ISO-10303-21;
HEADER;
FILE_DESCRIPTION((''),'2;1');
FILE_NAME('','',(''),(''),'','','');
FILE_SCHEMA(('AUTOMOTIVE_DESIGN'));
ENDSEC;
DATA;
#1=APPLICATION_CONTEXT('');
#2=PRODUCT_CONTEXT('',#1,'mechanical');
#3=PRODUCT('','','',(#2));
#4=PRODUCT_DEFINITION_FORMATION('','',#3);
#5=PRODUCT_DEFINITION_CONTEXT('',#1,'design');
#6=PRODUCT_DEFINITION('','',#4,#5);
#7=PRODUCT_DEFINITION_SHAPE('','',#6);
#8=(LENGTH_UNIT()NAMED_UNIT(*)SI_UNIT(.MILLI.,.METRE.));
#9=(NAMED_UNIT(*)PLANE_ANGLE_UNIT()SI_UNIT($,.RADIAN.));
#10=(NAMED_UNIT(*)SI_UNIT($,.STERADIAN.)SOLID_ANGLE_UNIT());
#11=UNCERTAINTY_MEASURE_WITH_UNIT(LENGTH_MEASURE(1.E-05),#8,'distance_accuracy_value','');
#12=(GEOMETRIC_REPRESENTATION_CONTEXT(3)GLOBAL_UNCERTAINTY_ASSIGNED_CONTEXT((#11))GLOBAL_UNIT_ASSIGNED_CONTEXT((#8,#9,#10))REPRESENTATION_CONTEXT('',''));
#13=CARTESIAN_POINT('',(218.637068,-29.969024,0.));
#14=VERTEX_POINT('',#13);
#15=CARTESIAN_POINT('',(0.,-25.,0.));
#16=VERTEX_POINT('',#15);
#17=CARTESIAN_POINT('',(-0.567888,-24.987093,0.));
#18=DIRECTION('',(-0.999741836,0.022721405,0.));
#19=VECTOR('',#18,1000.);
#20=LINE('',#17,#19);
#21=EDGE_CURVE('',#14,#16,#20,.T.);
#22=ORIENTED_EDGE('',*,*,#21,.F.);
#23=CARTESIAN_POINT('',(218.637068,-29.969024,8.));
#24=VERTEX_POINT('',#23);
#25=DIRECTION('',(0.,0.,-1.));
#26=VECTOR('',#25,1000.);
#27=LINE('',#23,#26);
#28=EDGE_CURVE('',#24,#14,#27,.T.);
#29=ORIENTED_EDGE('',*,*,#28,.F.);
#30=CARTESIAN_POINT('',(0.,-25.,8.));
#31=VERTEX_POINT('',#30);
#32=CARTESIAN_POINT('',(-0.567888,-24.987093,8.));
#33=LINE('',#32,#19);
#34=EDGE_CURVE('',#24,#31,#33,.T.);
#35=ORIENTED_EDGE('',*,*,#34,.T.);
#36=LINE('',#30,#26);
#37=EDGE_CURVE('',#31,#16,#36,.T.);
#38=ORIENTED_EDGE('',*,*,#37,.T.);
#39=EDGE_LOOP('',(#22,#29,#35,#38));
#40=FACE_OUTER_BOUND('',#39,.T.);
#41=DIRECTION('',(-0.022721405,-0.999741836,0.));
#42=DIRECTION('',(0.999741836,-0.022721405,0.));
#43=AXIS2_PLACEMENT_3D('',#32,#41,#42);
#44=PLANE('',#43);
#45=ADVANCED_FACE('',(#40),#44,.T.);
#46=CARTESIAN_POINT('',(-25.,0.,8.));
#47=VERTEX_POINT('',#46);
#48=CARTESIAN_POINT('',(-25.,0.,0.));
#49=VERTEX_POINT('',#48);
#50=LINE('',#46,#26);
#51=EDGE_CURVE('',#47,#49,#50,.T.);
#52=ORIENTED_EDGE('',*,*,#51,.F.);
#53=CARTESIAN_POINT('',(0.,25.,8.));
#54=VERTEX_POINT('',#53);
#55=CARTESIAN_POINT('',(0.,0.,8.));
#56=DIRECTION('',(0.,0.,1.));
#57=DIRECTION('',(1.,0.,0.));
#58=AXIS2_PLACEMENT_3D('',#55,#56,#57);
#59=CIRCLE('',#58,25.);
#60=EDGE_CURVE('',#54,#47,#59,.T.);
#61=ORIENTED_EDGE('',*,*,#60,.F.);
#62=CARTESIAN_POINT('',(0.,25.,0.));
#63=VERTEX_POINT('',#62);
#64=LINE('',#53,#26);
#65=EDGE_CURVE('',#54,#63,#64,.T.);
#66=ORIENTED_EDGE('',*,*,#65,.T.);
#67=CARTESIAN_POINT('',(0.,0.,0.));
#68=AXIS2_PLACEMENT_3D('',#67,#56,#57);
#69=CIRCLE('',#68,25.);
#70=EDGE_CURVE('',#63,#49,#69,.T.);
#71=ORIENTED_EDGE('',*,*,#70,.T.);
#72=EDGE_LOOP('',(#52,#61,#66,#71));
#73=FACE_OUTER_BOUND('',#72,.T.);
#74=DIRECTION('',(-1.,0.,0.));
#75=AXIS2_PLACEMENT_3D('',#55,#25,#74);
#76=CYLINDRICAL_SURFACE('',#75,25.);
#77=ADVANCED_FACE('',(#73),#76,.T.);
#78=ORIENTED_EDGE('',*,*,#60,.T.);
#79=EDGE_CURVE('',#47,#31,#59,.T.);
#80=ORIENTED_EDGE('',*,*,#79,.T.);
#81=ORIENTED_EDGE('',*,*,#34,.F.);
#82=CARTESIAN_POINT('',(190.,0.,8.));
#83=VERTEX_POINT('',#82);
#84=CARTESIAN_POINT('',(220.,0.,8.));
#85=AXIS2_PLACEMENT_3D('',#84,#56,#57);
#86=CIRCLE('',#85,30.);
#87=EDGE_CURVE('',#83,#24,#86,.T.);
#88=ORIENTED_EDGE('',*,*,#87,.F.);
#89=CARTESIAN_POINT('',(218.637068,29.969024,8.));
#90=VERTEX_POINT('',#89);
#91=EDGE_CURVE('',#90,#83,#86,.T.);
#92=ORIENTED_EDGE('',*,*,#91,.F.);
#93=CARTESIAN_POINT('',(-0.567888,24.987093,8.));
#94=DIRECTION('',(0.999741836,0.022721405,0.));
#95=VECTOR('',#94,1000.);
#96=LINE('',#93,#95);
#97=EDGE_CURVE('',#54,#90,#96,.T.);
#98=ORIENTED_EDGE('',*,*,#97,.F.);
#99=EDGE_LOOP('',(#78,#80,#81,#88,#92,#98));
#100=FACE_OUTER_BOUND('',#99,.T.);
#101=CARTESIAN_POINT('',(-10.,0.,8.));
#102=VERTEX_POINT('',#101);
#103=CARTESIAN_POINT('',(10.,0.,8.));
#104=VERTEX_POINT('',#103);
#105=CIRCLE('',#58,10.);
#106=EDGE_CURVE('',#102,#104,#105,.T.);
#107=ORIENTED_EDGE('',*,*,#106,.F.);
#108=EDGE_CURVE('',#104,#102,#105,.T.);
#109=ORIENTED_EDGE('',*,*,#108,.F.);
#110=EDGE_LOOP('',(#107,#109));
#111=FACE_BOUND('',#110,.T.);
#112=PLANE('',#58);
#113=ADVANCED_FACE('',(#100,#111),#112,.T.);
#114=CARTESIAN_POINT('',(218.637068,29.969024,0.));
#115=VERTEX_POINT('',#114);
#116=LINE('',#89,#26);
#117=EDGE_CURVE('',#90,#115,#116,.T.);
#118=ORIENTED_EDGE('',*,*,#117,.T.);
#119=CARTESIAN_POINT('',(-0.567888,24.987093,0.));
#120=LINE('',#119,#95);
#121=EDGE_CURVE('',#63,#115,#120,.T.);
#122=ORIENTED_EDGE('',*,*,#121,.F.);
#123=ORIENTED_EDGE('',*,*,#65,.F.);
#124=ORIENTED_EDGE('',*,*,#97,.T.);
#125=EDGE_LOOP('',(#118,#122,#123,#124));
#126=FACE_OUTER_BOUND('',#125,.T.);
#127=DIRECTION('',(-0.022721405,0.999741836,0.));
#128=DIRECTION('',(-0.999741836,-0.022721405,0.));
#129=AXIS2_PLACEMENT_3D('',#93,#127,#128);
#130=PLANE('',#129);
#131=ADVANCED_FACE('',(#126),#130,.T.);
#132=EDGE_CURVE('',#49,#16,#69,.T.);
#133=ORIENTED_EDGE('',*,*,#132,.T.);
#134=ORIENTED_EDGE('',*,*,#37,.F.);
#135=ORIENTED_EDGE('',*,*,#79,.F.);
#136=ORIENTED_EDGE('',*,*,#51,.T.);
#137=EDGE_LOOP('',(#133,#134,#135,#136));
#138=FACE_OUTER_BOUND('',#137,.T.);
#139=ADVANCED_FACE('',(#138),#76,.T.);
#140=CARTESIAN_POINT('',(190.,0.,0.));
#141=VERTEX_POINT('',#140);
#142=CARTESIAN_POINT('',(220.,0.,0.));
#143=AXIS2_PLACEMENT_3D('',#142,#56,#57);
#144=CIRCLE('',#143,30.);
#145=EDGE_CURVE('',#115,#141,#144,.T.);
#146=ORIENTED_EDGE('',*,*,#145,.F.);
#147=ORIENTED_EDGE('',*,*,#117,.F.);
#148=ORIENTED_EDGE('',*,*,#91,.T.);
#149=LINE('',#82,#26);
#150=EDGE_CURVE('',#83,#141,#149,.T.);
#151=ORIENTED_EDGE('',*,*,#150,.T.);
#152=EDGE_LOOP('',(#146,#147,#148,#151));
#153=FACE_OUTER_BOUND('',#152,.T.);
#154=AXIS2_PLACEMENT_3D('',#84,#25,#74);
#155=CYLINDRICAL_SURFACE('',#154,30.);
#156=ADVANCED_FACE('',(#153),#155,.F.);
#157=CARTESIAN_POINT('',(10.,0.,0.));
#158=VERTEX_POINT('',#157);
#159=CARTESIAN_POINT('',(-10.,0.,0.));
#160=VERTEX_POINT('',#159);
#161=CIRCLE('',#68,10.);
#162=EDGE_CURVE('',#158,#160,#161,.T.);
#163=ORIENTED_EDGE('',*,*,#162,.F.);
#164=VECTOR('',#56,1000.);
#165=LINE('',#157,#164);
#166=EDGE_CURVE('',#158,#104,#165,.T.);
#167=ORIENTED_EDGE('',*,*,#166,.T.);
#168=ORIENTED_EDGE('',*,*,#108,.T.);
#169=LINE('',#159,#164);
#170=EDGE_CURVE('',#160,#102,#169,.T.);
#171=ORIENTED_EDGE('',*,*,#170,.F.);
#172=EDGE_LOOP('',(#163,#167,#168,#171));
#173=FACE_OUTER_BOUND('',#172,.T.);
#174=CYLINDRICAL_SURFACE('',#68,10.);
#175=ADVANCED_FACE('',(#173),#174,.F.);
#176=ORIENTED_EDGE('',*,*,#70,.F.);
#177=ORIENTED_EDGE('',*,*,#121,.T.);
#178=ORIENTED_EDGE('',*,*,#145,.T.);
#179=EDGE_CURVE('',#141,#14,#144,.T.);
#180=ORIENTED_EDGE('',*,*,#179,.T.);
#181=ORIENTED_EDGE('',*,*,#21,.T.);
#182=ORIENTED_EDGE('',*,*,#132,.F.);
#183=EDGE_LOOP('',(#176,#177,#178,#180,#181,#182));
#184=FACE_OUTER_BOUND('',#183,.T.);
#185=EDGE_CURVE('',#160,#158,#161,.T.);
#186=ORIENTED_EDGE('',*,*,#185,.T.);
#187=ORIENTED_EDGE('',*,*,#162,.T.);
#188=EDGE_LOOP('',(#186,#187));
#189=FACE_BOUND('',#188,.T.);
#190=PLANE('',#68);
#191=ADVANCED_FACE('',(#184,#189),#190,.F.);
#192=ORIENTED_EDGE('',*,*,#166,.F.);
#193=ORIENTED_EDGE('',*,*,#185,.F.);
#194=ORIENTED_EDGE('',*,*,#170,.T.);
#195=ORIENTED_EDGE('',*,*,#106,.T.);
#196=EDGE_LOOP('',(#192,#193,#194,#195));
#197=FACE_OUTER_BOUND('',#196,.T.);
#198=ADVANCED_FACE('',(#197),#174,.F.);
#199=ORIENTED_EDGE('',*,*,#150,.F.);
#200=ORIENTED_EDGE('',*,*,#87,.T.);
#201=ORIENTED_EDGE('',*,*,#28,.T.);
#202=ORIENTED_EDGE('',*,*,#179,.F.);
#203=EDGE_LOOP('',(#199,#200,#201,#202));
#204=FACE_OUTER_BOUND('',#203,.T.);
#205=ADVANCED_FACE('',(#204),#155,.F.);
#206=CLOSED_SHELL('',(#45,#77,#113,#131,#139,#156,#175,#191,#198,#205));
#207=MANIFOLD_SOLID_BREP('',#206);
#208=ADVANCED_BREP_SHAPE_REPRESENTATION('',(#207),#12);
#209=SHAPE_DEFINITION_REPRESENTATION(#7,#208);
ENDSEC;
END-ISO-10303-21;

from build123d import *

# Parameters (mm, degrees)
EXTRUDE_1_DEPTH     = 8
SKETCH_2_R          = 10
CUT_EXTRUDE_1_DEPTH = 8


with BuildPart() as part:
    # 草图1 → 凸台-拉伸1 (new body)
    with BuildSketch(Plane.XY):
        with BuildLine():
            Line((218.63706763, 29.969024264), (0, 25))
            ThreePointArc((0, 25), (-25, 0), (0, -25))
            Line((0, -25), (218.63706763, -29.969024264))
            ThreePointArc((218.63706763, -29.969024264), (190, 0), (218.63706763, 29.969024264))
        make_face()
    extrude(amount=EXTRUDE_1_DEPTH)

    # 草图2 → 切除-拉伸1 (cut)
    with BuildSketch(Plane.XY.offset(8)):
        Circle(SKETCH_2_R)
    extrude(amount=-CUT_EXTRUDE_1_DEPTH, mode=Mode.SUBTRACT)


solid = part.part
